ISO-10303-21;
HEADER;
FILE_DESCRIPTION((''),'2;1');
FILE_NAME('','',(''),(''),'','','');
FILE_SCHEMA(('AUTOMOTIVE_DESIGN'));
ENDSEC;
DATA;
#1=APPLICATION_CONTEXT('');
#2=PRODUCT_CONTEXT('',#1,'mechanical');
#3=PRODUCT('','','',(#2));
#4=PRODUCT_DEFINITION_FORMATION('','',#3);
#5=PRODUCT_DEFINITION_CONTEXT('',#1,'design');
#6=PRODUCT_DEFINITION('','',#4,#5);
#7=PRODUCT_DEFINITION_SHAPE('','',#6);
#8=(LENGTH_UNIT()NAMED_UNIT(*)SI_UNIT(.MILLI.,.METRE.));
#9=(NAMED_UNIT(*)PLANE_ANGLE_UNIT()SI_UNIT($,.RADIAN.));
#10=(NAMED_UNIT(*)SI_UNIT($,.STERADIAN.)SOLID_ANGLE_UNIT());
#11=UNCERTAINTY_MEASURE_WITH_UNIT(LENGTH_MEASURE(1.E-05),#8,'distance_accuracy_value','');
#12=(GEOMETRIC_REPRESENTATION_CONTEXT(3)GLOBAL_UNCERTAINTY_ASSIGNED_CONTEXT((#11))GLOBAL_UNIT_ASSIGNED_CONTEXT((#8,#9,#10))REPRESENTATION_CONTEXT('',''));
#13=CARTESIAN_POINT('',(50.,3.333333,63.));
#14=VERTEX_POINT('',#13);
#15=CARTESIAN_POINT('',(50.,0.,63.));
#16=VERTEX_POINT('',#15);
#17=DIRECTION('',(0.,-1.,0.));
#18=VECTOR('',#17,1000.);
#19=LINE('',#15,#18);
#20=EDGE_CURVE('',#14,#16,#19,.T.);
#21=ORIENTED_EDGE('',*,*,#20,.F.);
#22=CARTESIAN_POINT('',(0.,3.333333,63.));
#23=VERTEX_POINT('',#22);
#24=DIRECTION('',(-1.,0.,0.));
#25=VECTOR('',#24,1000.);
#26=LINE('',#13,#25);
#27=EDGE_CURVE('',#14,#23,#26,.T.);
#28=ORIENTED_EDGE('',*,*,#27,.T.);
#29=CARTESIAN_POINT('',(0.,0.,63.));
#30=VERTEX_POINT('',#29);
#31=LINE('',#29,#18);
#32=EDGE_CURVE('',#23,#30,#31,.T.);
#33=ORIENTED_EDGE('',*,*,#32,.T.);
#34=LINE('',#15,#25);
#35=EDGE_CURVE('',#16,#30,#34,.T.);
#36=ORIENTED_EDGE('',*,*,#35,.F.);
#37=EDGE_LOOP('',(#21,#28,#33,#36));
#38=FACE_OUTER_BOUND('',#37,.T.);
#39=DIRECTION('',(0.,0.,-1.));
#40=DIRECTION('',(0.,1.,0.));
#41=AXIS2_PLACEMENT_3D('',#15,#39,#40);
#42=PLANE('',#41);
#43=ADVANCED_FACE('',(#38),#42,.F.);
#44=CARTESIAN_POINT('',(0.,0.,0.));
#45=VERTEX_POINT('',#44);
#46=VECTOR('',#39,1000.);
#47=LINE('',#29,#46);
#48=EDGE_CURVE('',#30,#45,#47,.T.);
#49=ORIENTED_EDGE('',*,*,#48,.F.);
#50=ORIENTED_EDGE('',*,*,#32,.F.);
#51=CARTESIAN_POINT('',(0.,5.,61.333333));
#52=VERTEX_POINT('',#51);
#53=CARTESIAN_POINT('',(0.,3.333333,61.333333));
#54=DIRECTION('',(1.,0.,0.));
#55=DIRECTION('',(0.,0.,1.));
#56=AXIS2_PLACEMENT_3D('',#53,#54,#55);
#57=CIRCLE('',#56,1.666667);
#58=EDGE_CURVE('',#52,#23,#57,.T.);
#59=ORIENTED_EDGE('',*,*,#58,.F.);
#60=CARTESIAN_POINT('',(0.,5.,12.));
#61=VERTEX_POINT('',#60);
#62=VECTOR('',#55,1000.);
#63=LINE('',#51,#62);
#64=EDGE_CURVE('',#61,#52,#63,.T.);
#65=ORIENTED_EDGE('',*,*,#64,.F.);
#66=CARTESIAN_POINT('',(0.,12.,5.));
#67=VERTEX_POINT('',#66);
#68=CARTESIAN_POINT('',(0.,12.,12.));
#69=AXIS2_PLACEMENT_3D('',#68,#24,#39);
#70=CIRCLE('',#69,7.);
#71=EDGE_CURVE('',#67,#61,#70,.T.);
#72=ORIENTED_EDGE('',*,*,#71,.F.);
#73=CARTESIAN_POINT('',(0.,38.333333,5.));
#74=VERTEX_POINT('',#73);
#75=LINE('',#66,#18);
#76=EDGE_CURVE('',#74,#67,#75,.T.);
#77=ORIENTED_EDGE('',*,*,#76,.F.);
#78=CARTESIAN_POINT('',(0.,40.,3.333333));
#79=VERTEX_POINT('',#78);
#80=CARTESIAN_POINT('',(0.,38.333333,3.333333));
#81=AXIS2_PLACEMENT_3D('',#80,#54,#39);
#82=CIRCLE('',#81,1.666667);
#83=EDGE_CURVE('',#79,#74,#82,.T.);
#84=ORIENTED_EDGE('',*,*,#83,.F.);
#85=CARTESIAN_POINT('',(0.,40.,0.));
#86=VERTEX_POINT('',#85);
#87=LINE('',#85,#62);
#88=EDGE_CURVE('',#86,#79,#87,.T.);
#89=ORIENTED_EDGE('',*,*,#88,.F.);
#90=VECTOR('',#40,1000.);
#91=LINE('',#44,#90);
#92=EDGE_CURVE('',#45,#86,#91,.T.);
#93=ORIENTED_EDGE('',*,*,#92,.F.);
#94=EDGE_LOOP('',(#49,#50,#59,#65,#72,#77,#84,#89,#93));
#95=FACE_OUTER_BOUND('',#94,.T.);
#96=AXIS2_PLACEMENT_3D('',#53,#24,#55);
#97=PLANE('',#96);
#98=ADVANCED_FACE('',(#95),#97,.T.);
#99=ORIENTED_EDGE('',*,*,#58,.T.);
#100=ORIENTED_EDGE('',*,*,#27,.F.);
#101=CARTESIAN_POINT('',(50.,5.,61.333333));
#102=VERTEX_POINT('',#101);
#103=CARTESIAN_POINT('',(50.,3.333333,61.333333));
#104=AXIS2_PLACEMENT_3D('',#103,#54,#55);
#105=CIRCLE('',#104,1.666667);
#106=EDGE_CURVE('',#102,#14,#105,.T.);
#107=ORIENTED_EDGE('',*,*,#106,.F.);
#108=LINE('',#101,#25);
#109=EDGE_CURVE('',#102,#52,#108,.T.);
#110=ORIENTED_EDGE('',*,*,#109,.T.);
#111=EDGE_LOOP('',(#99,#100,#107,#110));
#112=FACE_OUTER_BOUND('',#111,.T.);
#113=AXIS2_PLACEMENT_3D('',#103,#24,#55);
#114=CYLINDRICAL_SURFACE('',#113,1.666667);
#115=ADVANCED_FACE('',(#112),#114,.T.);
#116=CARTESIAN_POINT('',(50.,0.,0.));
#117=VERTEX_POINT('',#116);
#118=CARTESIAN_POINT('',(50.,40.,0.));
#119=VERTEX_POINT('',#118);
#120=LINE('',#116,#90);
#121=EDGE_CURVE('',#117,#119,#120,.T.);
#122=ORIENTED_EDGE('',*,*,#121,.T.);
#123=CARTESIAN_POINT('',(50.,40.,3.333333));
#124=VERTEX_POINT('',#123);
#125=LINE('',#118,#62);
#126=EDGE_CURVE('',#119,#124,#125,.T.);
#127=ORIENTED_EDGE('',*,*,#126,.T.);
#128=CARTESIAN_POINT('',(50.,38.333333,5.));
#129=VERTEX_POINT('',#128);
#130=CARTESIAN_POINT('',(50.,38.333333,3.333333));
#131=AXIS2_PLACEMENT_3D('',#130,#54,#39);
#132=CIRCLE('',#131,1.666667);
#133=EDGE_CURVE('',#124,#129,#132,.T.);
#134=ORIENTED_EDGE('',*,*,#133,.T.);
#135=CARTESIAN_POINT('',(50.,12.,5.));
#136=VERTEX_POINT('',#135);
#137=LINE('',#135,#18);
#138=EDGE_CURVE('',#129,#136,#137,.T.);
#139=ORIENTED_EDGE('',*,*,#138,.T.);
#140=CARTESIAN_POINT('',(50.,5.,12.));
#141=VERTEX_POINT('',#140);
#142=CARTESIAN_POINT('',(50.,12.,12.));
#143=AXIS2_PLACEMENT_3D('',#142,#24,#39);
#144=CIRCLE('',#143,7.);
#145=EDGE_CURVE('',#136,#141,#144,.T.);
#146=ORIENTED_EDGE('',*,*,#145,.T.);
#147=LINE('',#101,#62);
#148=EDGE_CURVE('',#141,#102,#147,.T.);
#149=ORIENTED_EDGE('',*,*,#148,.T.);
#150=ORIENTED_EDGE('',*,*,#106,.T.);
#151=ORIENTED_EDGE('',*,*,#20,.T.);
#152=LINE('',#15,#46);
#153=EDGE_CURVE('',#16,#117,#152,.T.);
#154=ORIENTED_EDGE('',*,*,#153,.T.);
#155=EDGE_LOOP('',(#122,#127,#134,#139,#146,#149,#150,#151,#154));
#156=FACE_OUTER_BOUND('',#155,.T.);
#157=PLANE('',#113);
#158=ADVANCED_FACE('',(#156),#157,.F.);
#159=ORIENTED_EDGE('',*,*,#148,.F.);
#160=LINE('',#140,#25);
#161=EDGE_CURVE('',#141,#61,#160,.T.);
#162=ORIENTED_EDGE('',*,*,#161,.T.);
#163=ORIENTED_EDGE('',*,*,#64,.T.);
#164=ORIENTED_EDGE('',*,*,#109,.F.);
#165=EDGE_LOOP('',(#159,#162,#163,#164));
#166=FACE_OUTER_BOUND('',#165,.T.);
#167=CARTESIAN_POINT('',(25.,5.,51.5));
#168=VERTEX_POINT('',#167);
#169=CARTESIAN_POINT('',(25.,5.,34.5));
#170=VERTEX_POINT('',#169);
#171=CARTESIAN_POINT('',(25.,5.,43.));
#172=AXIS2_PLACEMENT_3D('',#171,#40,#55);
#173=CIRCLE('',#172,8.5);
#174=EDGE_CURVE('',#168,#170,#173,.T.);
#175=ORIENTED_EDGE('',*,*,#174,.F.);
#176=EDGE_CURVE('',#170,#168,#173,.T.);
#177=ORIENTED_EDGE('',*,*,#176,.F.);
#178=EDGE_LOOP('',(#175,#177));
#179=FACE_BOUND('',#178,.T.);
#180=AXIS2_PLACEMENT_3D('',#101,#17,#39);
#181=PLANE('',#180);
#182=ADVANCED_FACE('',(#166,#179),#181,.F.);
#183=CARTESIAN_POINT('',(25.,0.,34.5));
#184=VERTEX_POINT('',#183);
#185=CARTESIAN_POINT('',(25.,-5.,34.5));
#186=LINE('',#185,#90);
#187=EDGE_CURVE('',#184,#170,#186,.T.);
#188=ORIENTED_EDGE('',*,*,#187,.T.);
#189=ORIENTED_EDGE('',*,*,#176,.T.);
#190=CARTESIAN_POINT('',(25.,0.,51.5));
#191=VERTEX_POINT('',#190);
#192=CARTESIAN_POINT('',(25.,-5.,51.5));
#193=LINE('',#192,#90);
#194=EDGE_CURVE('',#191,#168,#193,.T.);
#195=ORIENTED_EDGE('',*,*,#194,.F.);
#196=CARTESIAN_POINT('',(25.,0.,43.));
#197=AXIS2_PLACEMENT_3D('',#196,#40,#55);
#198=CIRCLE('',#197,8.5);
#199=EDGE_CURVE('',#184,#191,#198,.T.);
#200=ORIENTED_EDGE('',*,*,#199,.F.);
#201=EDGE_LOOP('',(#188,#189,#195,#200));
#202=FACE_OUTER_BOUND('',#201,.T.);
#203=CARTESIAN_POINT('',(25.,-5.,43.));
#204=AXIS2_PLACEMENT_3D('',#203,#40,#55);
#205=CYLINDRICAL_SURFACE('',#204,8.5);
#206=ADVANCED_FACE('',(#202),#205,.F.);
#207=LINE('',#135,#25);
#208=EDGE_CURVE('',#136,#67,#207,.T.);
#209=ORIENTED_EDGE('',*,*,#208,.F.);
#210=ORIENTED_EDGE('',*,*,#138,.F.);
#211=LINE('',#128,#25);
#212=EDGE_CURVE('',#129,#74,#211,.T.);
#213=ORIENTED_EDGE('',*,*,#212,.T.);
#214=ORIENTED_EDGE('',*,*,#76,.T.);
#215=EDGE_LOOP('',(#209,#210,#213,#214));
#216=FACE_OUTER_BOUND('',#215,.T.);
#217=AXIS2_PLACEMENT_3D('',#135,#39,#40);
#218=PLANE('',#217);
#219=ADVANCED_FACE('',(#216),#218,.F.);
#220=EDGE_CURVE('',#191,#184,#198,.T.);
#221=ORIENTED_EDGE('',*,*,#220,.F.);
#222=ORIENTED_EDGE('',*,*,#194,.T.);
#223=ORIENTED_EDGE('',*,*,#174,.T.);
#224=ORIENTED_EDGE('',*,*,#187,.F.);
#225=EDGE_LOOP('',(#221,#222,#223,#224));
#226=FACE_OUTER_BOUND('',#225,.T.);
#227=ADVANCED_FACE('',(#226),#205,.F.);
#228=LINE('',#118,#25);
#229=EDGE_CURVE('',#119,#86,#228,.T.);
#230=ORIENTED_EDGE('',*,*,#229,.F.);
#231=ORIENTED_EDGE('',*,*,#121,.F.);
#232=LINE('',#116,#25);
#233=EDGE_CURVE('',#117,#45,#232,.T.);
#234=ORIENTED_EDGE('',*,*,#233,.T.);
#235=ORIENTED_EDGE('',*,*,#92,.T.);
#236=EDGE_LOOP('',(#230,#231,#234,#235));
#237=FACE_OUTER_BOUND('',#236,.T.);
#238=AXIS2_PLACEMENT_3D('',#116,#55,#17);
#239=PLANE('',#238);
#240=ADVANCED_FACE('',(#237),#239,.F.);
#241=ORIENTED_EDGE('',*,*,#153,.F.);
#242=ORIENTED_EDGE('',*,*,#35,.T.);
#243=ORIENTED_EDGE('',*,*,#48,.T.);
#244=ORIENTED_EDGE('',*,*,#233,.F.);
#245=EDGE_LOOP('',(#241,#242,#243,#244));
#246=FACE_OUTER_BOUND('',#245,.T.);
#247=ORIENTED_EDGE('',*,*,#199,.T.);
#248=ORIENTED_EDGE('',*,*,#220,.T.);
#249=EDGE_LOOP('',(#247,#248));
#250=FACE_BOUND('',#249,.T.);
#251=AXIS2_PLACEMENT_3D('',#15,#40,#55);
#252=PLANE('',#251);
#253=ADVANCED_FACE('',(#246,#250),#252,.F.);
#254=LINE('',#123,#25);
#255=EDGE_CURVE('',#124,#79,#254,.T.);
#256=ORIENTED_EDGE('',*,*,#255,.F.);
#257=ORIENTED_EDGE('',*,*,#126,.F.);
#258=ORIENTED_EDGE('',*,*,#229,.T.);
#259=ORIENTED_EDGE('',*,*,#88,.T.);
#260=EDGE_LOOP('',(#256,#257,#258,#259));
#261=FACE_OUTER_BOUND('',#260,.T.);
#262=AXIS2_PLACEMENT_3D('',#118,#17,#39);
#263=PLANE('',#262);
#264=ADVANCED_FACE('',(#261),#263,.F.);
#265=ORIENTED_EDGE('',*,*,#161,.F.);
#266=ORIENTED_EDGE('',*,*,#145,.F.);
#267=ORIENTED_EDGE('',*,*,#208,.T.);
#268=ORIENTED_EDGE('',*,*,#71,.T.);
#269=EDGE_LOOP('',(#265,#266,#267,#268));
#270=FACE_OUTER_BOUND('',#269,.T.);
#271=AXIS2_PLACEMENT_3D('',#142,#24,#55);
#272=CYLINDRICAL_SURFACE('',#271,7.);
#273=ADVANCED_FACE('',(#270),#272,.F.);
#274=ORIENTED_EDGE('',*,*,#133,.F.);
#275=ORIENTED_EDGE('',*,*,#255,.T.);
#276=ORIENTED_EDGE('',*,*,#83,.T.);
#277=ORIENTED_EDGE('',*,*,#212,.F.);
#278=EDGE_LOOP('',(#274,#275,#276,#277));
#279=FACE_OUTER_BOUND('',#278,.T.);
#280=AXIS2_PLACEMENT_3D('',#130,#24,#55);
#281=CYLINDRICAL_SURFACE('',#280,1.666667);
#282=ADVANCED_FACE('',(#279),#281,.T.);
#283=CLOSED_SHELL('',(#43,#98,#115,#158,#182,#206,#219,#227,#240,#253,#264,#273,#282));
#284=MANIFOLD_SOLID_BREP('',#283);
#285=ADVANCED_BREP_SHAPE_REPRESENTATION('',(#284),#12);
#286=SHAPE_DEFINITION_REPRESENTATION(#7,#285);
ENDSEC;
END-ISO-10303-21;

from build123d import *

# Parameters (mm, degrees)
UNEQUAL_ANGLE_6_3_4_5_1_DEPTH = 50
SKETCH3_R                     = 8.5
CUT_EXTRUDE1_DEPTH            = 10


with BuildPart() as part:
    # Sketch1 → Unequal Angle 6.3-4-5(1) (new body)
    with BuildSketch(Plane(origin=(0, 0, 0), x_dir=(0, 0, 1), z_dir=(1, 0, 0))):
        with BuildLine():
            Line((63, 0), (0, 0))
            Line((0, 0), (0, -40))
            Line((0, -40), (3.333333333, -40))
            ThreePointArc((3.333333333, -40), (4.511844635, -39.511844635), (5, -38.333333333))
            Line((5, -38.333333333), (5, -12))
            ThreePointArc((5, -12), (7.050252532, -7.050252532), (12, -5))
            Line((12, -5), (61.333333333, -5))
            ThreePointArc((61.333333333, -5), (62.511844635, -4.511844635), (63, -3.333333333))
            Line((63, -3.333333333), (63, 0))
        make_face()
    extrude(amount=UNEQUAL_ANGLE_6_3_4_5_1_DEPTH)

    # Sketch3 → Cut-Extrude1 (cut)
    with BuildSketch(Plane(origin=(0, 5, 0), x_dir=(1, 0, 0), z_dir=(0, 1, 0))):
        with Locations(Location((25, -43, 0), (0, 0, 270))):
            Circle(SKETCH3_R)
    extrude(amount=-CUT_EXTRUDE1_DEPTH, mode=Mode.SUBTRACT)


solid = part.part
